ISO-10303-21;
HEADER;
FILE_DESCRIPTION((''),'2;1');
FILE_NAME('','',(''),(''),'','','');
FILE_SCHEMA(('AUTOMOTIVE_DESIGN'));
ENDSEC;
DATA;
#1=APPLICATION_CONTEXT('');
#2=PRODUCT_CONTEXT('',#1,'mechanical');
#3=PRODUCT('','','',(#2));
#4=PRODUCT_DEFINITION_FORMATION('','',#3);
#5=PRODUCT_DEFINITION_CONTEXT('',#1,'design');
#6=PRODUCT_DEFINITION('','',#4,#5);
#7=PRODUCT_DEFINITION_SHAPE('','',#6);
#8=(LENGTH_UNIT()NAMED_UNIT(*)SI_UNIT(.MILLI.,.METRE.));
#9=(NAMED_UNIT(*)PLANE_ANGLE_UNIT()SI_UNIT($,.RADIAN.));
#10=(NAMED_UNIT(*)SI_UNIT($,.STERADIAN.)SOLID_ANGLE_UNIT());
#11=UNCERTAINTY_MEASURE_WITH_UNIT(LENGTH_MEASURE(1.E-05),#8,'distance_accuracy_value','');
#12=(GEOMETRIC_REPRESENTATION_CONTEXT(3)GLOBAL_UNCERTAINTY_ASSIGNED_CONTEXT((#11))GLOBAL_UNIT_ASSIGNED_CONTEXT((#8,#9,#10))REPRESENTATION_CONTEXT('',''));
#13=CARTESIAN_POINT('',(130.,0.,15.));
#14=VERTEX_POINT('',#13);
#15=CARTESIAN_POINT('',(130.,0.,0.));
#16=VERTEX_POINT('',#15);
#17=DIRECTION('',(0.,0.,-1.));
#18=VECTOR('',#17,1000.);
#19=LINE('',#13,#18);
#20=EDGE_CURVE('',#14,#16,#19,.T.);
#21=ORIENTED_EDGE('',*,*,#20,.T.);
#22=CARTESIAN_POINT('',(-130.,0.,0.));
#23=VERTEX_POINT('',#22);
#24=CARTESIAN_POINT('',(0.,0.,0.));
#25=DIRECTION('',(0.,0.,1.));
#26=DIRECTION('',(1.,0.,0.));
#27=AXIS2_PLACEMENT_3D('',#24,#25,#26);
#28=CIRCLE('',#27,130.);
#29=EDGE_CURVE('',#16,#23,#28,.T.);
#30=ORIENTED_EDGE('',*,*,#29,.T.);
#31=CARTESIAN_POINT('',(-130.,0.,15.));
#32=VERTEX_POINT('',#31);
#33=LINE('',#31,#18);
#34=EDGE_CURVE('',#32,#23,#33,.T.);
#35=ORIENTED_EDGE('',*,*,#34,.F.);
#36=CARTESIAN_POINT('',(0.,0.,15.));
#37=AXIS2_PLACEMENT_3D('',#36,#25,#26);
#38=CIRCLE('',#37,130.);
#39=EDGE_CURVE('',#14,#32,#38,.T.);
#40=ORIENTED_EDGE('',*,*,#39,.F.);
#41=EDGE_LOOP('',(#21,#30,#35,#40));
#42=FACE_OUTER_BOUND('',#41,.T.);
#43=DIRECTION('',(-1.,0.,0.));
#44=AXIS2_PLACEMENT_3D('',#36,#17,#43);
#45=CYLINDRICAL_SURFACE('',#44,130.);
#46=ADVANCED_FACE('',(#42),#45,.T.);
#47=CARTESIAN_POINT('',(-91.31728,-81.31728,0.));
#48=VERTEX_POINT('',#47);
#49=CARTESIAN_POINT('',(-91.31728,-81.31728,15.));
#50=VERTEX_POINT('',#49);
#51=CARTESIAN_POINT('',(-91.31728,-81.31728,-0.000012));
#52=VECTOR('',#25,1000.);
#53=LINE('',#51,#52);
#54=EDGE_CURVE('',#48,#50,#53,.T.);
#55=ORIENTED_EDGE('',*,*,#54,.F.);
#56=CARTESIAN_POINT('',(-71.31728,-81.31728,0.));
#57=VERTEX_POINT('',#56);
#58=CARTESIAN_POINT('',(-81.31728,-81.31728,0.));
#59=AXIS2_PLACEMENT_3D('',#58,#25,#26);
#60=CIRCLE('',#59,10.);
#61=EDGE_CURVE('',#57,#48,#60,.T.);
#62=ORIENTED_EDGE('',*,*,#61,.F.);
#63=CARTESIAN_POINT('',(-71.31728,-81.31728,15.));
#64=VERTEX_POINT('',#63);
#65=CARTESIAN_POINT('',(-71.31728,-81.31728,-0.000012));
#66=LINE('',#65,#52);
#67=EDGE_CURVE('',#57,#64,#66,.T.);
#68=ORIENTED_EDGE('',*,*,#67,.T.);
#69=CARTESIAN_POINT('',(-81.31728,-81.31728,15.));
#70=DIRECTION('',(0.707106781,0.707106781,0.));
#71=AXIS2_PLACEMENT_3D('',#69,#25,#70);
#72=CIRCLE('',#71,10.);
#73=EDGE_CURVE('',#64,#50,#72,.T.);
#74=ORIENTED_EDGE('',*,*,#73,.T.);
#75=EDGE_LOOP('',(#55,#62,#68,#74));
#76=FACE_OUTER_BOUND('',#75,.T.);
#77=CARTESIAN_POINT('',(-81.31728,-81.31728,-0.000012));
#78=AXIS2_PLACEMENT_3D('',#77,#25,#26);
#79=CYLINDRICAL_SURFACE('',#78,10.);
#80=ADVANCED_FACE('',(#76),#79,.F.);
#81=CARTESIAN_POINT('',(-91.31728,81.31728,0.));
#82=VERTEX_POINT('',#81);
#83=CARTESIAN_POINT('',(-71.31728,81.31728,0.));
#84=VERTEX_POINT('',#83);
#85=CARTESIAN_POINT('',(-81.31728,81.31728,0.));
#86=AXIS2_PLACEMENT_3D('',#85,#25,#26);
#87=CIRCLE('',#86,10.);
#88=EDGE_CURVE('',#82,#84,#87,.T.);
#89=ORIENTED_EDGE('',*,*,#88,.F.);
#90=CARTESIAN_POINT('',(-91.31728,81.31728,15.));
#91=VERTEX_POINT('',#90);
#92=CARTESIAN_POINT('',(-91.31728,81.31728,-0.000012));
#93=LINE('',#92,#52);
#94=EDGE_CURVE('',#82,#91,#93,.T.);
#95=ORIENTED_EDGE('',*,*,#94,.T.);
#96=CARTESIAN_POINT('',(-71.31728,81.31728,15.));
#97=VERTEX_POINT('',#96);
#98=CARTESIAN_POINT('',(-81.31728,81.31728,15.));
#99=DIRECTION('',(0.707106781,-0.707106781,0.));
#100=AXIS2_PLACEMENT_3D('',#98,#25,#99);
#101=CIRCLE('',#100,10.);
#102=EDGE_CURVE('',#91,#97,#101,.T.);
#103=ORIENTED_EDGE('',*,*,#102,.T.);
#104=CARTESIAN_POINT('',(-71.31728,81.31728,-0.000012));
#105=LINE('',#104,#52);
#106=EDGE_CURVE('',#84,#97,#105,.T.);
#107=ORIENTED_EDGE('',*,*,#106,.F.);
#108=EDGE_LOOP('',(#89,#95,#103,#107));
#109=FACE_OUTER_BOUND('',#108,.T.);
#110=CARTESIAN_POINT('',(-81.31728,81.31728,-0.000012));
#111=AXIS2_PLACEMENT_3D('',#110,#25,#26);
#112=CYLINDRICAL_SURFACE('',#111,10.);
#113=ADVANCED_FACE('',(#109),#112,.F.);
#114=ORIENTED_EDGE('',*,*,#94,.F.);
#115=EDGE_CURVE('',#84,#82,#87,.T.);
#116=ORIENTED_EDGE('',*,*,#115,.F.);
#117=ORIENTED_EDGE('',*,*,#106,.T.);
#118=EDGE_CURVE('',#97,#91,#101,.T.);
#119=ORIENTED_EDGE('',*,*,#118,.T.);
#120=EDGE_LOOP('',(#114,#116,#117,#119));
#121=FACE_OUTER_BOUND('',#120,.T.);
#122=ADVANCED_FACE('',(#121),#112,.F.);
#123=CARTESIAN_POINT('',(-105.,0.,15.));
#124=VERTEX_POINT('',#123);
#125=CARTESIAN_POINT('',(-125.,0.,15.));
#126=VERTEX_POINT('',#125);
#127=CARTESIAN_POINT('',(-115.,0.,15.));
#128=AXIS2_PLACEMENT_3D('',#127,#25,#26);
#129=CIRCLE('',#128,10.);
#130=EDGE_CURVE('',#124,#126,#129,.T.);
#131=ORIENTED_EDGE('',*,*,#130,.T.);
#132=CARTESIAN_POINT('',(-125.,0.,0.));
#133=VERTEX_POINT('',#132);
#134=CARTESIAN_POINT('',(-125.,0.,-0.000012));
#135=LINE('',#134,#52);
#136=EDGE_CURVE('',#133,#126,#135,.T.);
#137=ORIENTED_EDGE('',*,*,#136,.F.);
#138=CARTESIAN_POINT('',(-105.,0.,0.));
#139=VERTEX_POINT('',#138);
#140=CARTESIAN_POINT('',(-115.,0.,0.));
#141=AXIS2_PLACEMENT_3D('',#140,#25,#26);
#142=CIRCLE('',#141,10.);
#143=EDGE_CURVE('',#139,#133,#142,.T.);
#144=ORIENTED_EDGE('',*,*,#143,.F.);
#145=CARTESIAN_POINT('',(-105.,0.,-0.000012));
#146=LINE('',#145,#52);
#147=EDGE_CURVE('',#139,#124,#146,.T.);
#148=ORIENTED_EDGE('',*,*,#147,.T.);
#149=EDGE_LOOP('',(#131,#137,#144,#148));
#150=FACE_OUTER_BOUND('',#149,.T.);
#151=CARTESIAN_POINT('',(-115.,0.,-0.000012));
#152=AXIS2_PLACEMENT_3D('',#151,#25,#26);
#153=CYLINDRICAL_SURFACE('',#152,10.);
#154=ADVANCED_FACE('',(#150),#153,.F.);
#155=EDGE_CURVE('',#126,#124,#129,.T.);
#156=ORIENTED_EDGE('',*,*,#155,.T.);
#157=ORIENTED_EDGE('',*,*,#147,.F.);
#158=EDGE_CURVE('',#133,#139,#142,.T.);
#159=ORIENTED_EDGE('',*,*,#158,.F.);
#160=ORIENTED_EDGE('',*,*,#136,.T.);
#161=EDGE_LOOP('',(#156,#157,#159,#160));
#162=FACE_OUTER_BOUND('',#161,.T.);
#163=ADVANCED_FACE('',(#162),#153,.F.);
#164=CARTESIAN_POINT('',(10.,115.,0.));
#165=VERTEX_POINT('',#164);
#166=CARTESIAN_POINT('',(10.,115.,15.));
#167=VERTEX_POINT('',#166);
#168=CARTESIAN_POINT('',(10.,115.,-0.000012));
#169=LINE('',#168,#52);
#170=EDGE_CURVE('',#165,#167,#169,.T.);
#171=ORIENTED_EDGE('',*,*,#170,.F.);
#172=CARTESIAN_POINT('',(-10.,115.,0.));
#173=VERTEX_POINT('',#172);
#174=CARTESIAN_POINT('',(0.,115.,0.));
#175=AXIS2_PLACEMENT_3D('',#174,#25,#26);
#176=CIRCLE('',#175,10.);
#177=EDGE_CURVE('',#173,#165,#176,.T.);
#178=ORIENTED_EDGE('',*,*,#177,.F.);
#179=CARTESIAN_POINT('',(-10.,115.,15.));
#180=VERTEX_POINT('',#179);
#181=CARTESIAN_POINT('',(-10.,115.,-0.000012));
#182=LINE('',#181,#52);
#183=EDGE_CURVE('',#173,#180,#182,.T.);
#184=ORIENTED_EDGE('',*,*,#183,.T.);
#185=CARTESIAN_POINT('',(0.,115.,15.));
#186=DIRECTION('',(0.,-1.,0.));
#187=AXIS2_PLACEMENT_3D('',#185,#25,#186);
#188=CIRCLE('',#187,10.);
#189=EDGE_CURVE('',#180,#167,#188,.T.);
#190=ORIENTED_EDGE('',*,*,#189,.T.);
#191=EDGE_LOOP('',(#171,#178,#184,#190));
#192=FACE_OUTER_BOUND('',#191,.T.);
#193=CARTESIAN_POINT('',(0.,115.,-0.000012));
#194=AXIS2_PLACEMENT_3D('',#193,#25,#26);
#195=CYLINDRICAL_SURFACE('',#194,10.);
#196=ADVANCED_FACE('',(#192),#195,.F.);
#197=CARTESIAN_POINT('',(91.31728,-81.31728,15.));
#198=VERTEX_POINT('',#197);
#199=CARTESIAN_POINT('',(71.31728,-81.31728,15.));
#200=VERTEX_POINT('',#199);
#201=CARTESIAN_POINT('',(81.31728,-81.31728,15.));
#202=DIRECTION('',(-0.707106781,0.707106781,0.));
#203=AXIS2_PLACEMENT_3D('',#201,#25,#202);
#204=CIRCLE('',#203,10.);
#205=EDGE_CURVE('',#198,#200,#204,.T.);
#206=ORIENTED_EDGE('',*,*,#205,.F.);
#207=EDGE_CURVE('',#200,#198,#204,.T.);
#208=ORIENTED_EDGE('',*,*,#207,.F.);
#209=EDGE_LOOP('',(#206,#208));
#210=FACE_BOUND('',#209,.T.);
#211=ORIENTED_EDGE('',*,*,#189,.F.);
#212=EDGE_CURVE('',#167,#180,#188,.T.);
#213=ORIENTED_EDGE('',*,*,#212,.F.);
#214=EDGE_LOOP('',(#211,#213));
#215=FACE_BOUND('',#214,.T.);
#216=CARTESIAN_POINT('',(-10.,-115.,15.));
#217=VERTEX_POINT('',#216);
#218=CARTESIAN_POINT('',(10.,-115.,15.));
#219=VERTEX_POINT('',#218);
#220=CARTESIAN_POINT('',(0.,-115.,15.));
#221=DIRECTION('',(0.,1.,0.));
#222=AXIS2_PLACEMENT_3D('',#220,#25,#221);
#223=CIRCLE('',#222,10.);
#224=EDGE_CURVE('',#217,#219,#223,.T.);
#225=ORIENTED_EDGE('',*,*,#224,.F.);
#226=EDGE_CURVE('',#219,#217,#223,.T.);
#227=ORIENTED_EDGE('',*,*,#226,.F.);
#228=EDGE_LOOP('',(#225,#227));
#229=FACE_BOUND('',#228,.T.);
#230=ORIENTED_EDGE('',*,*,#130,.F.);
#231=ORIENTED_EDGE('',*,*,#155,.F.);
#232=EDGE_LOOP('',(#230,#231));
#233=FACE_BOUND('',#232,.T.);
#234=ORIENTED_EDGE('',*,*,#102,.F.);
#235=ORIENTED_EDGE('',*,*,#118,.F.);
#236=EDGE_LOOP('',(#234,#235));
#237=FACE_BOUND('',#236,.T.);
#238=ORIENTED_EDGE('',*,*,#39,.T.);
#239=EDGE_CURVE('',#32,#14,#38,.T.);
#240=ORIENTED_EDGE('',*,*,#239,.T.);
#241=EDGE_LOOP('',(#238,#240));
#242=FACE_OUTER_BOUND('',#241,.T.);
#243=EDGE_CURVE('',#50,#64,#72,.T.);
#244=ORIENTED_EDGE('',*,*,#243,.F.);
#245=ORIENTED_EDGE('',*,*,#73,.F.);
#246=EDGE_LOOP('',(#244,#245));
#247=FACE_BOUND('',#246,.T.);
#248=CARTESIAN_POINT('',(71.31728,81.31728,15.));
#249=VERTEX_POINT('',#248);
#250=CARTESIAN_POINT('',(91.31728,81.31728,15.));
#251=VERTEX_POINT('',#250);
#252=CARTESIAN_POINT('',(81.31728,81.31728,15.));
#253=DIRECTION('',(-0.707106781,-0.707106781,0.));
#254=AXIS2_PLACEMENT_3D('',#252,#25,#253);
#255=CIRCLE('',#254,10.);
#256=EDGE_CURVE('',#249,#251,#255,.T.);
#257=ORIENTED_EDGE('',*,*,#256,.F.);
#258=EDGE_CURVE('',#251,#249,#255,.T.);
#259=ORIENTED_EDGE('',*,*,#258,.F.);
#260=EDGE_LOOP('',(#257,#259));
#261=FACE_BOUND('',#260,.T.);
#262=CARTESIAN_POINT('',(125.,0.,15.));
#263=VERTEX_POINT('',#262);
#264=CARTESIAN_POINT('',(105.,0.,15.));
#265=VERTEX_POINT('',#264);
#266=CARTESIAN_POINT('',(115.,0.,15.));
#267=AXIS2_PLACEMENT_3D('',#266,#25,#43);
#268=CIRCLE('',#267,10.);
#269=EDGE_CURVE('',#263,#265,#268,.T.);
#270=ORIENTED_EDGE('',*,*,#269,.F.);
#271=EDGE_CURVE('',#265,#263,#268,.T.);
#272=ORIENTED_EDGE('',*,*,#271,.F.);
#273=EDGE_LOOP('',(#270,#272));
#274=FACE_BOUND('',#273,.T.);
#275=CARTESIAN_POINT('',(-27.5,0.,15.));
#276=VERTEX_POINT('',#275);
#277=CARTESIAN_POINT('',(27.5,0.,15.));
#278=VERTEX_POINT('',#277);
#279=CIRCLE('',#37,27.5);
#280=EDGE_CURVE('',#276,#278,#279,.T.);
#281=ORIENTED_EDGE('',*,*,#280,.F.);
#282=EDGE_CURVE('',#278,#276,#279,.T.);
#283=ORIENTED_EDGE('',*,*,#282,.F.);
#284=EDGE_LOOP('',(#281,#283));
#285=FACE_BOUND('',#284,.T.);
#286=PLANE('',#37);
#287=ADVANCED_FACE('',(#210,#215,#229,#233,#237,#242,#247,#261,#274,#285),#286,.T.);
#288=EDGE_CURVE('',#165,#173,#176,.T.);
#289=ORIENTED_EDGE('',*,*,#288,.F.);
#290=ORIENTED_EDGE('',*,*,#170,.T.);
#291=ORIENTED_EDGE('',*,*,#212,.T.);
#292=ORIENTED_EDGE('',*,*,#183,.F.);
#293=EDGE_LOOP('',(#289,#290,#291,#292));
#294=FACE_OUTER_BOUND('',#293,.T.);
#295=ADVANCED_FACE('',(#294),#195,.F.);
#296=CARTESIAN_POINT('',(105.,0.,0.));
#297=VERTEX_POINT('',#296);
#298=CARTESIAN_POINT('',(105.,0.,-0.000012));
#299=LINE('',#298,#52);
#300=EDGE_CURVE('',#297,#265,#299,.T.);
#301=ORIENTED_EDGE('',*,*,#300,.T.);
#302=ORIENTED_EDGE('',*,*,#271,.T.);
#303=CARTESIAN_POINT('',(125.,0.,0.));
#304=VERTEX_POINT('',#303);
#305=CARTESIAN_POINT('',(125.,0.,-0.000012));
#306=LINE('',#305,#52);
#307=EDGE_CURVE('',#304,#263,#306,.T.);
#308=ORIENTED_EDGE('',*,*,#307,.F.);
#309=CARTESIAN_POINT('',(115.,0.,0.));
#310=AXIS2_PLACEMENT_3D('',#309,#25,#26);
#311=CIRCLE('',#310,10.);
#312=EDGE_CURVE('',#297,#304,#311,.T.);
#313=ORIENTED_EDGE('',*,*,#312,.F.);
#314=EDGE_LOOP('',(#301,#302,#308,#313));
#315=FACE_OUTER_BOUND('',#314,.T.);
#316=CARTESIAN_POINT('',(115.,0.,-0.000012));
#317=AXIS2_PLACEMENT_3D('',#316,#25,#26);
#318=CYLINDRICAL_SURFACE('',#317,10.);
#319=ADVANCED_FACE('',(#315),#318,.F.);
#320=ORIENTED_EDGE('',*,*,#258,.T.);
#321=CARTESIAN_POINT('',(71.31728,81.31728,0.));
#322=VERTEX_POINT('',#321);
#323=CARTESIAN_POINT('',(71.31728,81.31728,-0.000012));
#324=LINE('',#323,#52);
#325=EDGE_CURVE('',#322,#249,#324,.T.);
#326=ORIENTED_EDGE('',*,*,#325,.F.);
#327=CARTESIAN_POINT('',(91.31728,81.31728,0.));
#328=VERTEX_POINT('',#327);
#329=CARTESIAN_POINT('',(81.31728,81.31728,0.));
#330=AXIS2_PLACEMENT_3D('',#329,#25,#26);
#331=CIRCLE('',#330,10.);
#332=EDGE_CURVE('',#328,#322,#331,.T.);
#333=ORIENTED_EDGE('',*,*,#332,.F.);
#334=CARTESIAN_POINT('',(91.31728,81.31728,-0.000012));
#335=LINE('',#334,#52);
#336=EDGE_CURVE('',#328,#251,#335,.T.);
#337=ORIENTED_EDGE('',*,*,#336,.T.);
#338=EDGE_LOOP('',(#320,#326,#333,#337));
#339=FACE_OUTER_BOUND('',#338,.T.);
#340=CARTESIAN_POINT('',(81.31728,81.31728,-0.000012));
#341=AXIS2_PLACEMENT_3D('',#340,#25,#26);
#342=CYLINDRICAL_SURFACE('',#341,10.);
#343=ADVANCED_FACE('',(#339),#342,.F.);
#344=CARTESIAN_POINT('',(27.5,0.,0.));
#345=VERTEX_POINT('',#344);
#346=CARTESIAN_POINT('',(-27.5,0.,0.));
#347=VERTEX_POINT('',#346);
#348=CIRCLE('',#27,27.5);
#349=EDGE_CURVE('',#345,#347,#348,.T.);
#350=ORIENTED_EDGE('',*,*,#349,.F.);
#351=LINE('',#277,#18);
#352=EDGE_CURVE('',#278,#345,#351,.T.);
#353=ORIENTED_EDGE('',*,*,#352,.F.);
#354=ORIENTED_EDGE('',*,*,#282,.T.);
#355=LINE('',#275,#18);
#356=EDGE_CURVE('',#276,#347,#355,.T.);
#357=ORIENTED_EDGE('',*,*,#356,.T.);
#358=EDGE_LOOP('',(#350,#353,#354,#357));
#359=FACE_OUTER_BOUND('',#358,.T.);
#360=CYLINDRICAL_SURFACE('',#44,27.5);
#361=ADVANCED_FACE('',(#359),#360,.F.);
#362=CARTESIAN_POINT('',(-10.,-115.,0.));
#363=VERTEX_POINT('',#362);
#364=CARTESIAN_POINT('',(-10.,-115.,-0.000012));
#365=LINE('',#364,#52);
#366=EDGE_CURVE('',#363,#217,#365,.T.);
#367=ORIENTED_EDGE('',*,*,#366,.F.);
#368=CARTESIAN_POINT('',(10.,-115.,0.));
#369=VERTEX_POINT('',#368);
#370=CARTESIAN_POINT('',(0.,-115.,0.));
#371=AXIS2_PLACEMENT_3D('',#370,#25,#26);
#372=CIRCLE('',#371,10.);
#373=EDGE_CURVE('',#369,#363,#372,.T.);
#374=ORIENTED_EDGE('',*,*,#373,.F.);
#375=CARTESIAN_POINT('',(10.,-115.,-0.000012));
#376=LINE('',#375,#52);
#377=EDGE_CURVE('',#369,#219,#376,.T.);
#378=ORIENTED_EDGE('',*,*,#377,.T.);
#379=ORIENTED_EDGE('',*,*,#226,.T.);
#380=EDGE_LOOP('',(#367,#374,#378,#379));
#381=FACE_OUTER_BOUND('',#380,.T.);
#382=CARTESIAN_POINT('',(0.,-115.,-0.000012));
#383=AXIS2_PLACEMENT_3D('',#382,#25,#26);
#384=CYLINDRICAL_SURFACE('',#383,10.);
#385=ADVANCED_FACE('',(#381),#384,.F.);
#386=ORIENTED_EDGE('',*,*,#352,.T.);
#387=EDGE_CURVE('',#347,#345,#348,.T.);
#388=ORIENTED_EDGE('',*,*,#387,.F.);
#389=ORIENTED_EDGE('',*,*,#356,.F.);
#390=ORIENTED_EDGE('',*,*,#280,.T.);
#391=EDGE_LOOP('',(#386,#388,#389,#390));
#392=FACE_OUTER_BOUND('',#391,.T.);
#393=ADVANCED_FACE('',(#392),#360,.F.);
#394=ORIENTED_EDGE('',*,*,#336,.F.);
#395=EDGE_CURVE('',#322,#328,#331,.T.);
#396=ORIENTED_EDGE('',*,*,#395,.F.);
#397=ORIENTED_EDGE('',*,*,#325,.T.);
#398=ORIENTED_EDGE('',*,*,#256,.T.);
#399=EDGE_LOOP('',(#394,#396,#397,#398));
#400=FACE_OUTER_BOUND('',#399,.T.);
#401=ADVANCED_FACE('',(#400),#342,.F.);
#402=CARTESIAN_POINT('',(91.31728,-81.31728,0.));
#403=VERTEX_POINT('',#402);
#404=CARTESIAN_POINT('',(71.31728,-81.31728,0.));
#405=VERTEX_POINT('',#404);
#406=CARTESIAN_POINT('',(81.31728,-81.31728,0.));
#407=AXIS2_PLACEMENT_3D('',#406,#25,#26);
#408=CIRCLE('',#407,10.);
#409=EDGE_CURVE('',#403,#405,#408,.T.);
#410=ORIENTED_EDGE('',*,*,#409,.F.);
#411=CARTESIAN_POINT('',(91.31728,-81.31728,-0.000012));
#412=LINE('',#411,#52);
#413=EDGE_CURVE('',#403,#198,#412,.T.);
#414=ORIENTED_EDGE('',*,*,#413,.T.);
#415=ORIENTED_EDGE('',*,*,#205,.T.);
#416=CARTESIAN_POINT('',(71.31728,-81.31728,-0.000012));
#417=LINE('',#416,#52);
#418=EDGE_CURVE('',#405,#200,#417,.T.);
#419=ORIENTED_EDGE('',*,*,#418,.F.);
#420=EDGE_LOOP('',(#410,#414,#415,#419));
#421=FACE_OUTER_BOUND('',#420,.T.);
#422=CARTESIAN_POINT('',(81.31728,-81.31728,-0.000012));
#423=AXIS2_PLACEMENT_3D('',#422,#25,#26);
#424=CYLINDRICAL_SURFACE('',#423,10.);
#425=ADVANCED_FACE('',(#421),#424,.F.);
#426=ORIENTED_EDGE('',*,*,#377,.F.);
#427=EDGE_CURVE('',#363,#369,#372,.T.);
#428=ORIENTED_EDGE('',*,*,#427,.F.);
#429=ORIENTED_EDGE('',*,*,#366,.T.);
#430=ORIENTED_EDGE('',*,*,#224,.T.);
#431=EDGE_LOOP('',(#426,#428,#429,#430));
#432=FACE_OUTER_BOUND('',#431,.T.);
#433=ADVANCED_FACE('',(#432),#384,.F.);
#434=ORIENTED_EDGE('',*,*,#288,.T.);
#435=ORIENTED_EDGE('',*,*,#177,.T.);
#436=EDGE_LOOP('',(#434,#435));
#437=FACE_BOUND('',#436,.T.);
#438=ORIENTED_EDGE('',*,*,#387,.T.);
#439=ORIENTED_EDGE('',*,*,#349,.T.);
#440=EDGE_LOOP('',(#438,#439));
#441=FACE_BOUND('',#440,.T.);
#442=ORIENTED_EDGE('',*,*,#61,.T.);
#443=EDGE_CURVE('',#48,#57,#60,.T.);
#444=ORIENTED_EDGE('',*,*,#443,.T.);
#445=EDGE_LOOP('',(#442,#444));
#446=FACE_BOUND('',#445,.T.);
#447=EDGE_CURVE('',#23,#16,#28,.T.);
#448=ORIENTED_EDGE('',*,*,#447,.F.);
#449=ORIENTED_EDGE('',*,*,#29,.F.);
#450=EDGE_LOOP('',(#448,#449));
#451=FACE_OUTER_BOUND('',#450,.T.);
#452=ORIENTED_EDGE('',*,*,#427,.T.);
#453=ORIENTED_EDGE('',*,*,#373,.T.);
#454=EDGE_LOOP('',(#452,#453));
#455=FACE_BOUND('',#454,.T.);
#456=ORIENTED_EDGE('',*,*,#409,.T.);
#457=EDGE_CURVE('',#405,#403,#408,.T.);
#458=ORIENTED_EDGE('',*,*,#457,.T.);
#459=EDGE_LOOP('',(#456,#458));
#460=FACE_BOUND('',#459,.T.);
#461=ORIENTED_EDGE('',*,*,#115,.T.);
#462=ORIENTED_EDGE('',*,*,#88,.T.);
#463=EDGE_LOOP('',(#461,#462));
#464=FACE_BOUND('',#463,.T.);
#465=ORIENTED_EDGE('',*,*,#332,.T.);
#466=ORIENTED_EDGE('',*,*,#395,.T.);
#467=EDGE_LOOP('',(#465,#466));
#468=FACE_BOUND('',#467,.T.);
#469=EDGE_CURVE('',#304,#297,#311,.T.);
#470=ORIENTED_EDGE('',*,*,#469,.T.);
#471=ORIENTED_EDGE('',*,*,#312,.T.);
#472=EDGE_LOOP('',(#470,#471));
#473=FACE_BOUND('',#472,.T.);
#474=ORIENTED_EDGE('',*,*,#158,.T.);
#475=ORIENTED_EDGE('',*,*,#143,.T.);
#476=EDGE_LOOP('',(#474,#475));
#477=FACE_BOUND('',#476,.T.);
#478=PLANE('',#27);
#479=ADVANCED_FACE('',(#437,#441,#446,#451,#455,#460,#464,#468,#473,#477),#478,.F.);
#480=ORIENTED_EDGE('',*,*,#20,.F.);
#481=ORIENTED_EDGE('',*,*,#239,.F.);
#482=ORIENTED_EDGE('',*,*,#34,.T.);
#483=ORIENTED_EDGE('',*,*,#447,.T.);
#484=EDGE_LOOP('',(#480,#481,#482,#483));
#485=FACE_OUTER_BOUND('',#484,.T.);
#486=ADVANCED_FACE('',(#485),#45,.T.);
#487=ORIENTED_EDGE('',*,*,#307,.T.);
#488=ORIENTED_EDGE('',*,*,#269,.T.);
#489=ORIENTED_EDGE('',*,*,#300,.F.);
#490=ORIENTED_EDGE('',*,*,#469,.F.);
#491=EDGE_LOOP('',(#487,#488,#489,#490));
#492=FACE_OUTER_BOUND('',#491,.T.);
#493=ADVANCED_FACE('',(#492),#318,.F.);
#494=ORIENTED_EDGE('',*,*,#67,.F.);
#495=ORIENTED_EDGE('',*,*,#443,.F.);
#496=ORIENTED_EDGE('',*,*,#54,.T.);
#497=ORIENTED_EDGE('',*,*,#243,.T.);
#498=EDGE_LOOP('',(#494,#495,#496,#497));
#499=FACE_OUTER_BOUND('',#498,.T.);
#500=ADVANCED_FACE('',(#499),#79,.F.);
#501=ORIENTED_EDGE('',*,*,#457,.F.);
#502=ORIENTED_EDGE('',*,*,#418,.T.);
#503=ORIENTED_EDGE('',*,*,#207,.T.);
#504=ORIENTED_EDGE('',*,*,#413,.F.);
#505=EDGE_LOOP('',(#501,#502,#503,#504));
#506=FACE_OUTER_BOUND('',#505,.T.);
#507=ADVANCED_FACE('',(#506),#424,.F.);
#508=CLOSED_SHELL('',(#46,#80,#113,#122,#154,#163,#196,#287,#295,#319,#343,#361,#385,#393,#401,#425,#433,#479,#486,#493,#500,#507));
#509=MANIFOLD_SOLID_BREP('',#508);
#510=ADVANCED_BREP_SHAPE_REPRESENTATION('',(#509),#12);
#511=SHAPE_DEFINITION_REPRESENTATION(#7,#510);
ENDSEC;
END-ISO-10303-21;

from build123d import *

# Parameters (mm, degrees)
SKETCH2_R           = 130
SKETCH2_R_2         = 27.5
BOSS_EXTRUDE1_DEPTH = 15
SKETCH3_R           = 10
CUT_EXTRUDE1_DEPTH  = 185.458667457
CIRPATTERN1_COUNT   = 8


with BuildPart() as part:
    # Sketch2 → Boss-Extrude1 (new body)
    with BuildSketch(Plane.XY):
        Circle(SKETCH2_R)
        Circle(SKETCH2_R_2, mode=Mode.SUBTRACT)
    extrude(amount=BOSS_EXTRUDE1_DEPTH)

    # Sketch3 → Cut-Extrude1 (cut, symmetric)
    with BuildSketch(Plane.XY):
        with Locations((-115, 0)):
            Circle(SKETCH3_R)
    cut_extrude1 = extrude(amount=CUT_EXTRUDE1_DEPTH, both=True, mode=Mode.SUBTRACT)

    # CirPattern1: Cut-Extrude1 ×8 about axis
    cirpattern1_axis = Axis((0, 0, 0), (0, 0, 1))
    for i in range(1, CIRPATTERN1_COUNT):
        add(cut_extrude1.rotate(cirpattern1_axis, i * 360 / CIRPATTERN1_COUNT), mode=Mode.SUBTRACT)


solid = part.part
